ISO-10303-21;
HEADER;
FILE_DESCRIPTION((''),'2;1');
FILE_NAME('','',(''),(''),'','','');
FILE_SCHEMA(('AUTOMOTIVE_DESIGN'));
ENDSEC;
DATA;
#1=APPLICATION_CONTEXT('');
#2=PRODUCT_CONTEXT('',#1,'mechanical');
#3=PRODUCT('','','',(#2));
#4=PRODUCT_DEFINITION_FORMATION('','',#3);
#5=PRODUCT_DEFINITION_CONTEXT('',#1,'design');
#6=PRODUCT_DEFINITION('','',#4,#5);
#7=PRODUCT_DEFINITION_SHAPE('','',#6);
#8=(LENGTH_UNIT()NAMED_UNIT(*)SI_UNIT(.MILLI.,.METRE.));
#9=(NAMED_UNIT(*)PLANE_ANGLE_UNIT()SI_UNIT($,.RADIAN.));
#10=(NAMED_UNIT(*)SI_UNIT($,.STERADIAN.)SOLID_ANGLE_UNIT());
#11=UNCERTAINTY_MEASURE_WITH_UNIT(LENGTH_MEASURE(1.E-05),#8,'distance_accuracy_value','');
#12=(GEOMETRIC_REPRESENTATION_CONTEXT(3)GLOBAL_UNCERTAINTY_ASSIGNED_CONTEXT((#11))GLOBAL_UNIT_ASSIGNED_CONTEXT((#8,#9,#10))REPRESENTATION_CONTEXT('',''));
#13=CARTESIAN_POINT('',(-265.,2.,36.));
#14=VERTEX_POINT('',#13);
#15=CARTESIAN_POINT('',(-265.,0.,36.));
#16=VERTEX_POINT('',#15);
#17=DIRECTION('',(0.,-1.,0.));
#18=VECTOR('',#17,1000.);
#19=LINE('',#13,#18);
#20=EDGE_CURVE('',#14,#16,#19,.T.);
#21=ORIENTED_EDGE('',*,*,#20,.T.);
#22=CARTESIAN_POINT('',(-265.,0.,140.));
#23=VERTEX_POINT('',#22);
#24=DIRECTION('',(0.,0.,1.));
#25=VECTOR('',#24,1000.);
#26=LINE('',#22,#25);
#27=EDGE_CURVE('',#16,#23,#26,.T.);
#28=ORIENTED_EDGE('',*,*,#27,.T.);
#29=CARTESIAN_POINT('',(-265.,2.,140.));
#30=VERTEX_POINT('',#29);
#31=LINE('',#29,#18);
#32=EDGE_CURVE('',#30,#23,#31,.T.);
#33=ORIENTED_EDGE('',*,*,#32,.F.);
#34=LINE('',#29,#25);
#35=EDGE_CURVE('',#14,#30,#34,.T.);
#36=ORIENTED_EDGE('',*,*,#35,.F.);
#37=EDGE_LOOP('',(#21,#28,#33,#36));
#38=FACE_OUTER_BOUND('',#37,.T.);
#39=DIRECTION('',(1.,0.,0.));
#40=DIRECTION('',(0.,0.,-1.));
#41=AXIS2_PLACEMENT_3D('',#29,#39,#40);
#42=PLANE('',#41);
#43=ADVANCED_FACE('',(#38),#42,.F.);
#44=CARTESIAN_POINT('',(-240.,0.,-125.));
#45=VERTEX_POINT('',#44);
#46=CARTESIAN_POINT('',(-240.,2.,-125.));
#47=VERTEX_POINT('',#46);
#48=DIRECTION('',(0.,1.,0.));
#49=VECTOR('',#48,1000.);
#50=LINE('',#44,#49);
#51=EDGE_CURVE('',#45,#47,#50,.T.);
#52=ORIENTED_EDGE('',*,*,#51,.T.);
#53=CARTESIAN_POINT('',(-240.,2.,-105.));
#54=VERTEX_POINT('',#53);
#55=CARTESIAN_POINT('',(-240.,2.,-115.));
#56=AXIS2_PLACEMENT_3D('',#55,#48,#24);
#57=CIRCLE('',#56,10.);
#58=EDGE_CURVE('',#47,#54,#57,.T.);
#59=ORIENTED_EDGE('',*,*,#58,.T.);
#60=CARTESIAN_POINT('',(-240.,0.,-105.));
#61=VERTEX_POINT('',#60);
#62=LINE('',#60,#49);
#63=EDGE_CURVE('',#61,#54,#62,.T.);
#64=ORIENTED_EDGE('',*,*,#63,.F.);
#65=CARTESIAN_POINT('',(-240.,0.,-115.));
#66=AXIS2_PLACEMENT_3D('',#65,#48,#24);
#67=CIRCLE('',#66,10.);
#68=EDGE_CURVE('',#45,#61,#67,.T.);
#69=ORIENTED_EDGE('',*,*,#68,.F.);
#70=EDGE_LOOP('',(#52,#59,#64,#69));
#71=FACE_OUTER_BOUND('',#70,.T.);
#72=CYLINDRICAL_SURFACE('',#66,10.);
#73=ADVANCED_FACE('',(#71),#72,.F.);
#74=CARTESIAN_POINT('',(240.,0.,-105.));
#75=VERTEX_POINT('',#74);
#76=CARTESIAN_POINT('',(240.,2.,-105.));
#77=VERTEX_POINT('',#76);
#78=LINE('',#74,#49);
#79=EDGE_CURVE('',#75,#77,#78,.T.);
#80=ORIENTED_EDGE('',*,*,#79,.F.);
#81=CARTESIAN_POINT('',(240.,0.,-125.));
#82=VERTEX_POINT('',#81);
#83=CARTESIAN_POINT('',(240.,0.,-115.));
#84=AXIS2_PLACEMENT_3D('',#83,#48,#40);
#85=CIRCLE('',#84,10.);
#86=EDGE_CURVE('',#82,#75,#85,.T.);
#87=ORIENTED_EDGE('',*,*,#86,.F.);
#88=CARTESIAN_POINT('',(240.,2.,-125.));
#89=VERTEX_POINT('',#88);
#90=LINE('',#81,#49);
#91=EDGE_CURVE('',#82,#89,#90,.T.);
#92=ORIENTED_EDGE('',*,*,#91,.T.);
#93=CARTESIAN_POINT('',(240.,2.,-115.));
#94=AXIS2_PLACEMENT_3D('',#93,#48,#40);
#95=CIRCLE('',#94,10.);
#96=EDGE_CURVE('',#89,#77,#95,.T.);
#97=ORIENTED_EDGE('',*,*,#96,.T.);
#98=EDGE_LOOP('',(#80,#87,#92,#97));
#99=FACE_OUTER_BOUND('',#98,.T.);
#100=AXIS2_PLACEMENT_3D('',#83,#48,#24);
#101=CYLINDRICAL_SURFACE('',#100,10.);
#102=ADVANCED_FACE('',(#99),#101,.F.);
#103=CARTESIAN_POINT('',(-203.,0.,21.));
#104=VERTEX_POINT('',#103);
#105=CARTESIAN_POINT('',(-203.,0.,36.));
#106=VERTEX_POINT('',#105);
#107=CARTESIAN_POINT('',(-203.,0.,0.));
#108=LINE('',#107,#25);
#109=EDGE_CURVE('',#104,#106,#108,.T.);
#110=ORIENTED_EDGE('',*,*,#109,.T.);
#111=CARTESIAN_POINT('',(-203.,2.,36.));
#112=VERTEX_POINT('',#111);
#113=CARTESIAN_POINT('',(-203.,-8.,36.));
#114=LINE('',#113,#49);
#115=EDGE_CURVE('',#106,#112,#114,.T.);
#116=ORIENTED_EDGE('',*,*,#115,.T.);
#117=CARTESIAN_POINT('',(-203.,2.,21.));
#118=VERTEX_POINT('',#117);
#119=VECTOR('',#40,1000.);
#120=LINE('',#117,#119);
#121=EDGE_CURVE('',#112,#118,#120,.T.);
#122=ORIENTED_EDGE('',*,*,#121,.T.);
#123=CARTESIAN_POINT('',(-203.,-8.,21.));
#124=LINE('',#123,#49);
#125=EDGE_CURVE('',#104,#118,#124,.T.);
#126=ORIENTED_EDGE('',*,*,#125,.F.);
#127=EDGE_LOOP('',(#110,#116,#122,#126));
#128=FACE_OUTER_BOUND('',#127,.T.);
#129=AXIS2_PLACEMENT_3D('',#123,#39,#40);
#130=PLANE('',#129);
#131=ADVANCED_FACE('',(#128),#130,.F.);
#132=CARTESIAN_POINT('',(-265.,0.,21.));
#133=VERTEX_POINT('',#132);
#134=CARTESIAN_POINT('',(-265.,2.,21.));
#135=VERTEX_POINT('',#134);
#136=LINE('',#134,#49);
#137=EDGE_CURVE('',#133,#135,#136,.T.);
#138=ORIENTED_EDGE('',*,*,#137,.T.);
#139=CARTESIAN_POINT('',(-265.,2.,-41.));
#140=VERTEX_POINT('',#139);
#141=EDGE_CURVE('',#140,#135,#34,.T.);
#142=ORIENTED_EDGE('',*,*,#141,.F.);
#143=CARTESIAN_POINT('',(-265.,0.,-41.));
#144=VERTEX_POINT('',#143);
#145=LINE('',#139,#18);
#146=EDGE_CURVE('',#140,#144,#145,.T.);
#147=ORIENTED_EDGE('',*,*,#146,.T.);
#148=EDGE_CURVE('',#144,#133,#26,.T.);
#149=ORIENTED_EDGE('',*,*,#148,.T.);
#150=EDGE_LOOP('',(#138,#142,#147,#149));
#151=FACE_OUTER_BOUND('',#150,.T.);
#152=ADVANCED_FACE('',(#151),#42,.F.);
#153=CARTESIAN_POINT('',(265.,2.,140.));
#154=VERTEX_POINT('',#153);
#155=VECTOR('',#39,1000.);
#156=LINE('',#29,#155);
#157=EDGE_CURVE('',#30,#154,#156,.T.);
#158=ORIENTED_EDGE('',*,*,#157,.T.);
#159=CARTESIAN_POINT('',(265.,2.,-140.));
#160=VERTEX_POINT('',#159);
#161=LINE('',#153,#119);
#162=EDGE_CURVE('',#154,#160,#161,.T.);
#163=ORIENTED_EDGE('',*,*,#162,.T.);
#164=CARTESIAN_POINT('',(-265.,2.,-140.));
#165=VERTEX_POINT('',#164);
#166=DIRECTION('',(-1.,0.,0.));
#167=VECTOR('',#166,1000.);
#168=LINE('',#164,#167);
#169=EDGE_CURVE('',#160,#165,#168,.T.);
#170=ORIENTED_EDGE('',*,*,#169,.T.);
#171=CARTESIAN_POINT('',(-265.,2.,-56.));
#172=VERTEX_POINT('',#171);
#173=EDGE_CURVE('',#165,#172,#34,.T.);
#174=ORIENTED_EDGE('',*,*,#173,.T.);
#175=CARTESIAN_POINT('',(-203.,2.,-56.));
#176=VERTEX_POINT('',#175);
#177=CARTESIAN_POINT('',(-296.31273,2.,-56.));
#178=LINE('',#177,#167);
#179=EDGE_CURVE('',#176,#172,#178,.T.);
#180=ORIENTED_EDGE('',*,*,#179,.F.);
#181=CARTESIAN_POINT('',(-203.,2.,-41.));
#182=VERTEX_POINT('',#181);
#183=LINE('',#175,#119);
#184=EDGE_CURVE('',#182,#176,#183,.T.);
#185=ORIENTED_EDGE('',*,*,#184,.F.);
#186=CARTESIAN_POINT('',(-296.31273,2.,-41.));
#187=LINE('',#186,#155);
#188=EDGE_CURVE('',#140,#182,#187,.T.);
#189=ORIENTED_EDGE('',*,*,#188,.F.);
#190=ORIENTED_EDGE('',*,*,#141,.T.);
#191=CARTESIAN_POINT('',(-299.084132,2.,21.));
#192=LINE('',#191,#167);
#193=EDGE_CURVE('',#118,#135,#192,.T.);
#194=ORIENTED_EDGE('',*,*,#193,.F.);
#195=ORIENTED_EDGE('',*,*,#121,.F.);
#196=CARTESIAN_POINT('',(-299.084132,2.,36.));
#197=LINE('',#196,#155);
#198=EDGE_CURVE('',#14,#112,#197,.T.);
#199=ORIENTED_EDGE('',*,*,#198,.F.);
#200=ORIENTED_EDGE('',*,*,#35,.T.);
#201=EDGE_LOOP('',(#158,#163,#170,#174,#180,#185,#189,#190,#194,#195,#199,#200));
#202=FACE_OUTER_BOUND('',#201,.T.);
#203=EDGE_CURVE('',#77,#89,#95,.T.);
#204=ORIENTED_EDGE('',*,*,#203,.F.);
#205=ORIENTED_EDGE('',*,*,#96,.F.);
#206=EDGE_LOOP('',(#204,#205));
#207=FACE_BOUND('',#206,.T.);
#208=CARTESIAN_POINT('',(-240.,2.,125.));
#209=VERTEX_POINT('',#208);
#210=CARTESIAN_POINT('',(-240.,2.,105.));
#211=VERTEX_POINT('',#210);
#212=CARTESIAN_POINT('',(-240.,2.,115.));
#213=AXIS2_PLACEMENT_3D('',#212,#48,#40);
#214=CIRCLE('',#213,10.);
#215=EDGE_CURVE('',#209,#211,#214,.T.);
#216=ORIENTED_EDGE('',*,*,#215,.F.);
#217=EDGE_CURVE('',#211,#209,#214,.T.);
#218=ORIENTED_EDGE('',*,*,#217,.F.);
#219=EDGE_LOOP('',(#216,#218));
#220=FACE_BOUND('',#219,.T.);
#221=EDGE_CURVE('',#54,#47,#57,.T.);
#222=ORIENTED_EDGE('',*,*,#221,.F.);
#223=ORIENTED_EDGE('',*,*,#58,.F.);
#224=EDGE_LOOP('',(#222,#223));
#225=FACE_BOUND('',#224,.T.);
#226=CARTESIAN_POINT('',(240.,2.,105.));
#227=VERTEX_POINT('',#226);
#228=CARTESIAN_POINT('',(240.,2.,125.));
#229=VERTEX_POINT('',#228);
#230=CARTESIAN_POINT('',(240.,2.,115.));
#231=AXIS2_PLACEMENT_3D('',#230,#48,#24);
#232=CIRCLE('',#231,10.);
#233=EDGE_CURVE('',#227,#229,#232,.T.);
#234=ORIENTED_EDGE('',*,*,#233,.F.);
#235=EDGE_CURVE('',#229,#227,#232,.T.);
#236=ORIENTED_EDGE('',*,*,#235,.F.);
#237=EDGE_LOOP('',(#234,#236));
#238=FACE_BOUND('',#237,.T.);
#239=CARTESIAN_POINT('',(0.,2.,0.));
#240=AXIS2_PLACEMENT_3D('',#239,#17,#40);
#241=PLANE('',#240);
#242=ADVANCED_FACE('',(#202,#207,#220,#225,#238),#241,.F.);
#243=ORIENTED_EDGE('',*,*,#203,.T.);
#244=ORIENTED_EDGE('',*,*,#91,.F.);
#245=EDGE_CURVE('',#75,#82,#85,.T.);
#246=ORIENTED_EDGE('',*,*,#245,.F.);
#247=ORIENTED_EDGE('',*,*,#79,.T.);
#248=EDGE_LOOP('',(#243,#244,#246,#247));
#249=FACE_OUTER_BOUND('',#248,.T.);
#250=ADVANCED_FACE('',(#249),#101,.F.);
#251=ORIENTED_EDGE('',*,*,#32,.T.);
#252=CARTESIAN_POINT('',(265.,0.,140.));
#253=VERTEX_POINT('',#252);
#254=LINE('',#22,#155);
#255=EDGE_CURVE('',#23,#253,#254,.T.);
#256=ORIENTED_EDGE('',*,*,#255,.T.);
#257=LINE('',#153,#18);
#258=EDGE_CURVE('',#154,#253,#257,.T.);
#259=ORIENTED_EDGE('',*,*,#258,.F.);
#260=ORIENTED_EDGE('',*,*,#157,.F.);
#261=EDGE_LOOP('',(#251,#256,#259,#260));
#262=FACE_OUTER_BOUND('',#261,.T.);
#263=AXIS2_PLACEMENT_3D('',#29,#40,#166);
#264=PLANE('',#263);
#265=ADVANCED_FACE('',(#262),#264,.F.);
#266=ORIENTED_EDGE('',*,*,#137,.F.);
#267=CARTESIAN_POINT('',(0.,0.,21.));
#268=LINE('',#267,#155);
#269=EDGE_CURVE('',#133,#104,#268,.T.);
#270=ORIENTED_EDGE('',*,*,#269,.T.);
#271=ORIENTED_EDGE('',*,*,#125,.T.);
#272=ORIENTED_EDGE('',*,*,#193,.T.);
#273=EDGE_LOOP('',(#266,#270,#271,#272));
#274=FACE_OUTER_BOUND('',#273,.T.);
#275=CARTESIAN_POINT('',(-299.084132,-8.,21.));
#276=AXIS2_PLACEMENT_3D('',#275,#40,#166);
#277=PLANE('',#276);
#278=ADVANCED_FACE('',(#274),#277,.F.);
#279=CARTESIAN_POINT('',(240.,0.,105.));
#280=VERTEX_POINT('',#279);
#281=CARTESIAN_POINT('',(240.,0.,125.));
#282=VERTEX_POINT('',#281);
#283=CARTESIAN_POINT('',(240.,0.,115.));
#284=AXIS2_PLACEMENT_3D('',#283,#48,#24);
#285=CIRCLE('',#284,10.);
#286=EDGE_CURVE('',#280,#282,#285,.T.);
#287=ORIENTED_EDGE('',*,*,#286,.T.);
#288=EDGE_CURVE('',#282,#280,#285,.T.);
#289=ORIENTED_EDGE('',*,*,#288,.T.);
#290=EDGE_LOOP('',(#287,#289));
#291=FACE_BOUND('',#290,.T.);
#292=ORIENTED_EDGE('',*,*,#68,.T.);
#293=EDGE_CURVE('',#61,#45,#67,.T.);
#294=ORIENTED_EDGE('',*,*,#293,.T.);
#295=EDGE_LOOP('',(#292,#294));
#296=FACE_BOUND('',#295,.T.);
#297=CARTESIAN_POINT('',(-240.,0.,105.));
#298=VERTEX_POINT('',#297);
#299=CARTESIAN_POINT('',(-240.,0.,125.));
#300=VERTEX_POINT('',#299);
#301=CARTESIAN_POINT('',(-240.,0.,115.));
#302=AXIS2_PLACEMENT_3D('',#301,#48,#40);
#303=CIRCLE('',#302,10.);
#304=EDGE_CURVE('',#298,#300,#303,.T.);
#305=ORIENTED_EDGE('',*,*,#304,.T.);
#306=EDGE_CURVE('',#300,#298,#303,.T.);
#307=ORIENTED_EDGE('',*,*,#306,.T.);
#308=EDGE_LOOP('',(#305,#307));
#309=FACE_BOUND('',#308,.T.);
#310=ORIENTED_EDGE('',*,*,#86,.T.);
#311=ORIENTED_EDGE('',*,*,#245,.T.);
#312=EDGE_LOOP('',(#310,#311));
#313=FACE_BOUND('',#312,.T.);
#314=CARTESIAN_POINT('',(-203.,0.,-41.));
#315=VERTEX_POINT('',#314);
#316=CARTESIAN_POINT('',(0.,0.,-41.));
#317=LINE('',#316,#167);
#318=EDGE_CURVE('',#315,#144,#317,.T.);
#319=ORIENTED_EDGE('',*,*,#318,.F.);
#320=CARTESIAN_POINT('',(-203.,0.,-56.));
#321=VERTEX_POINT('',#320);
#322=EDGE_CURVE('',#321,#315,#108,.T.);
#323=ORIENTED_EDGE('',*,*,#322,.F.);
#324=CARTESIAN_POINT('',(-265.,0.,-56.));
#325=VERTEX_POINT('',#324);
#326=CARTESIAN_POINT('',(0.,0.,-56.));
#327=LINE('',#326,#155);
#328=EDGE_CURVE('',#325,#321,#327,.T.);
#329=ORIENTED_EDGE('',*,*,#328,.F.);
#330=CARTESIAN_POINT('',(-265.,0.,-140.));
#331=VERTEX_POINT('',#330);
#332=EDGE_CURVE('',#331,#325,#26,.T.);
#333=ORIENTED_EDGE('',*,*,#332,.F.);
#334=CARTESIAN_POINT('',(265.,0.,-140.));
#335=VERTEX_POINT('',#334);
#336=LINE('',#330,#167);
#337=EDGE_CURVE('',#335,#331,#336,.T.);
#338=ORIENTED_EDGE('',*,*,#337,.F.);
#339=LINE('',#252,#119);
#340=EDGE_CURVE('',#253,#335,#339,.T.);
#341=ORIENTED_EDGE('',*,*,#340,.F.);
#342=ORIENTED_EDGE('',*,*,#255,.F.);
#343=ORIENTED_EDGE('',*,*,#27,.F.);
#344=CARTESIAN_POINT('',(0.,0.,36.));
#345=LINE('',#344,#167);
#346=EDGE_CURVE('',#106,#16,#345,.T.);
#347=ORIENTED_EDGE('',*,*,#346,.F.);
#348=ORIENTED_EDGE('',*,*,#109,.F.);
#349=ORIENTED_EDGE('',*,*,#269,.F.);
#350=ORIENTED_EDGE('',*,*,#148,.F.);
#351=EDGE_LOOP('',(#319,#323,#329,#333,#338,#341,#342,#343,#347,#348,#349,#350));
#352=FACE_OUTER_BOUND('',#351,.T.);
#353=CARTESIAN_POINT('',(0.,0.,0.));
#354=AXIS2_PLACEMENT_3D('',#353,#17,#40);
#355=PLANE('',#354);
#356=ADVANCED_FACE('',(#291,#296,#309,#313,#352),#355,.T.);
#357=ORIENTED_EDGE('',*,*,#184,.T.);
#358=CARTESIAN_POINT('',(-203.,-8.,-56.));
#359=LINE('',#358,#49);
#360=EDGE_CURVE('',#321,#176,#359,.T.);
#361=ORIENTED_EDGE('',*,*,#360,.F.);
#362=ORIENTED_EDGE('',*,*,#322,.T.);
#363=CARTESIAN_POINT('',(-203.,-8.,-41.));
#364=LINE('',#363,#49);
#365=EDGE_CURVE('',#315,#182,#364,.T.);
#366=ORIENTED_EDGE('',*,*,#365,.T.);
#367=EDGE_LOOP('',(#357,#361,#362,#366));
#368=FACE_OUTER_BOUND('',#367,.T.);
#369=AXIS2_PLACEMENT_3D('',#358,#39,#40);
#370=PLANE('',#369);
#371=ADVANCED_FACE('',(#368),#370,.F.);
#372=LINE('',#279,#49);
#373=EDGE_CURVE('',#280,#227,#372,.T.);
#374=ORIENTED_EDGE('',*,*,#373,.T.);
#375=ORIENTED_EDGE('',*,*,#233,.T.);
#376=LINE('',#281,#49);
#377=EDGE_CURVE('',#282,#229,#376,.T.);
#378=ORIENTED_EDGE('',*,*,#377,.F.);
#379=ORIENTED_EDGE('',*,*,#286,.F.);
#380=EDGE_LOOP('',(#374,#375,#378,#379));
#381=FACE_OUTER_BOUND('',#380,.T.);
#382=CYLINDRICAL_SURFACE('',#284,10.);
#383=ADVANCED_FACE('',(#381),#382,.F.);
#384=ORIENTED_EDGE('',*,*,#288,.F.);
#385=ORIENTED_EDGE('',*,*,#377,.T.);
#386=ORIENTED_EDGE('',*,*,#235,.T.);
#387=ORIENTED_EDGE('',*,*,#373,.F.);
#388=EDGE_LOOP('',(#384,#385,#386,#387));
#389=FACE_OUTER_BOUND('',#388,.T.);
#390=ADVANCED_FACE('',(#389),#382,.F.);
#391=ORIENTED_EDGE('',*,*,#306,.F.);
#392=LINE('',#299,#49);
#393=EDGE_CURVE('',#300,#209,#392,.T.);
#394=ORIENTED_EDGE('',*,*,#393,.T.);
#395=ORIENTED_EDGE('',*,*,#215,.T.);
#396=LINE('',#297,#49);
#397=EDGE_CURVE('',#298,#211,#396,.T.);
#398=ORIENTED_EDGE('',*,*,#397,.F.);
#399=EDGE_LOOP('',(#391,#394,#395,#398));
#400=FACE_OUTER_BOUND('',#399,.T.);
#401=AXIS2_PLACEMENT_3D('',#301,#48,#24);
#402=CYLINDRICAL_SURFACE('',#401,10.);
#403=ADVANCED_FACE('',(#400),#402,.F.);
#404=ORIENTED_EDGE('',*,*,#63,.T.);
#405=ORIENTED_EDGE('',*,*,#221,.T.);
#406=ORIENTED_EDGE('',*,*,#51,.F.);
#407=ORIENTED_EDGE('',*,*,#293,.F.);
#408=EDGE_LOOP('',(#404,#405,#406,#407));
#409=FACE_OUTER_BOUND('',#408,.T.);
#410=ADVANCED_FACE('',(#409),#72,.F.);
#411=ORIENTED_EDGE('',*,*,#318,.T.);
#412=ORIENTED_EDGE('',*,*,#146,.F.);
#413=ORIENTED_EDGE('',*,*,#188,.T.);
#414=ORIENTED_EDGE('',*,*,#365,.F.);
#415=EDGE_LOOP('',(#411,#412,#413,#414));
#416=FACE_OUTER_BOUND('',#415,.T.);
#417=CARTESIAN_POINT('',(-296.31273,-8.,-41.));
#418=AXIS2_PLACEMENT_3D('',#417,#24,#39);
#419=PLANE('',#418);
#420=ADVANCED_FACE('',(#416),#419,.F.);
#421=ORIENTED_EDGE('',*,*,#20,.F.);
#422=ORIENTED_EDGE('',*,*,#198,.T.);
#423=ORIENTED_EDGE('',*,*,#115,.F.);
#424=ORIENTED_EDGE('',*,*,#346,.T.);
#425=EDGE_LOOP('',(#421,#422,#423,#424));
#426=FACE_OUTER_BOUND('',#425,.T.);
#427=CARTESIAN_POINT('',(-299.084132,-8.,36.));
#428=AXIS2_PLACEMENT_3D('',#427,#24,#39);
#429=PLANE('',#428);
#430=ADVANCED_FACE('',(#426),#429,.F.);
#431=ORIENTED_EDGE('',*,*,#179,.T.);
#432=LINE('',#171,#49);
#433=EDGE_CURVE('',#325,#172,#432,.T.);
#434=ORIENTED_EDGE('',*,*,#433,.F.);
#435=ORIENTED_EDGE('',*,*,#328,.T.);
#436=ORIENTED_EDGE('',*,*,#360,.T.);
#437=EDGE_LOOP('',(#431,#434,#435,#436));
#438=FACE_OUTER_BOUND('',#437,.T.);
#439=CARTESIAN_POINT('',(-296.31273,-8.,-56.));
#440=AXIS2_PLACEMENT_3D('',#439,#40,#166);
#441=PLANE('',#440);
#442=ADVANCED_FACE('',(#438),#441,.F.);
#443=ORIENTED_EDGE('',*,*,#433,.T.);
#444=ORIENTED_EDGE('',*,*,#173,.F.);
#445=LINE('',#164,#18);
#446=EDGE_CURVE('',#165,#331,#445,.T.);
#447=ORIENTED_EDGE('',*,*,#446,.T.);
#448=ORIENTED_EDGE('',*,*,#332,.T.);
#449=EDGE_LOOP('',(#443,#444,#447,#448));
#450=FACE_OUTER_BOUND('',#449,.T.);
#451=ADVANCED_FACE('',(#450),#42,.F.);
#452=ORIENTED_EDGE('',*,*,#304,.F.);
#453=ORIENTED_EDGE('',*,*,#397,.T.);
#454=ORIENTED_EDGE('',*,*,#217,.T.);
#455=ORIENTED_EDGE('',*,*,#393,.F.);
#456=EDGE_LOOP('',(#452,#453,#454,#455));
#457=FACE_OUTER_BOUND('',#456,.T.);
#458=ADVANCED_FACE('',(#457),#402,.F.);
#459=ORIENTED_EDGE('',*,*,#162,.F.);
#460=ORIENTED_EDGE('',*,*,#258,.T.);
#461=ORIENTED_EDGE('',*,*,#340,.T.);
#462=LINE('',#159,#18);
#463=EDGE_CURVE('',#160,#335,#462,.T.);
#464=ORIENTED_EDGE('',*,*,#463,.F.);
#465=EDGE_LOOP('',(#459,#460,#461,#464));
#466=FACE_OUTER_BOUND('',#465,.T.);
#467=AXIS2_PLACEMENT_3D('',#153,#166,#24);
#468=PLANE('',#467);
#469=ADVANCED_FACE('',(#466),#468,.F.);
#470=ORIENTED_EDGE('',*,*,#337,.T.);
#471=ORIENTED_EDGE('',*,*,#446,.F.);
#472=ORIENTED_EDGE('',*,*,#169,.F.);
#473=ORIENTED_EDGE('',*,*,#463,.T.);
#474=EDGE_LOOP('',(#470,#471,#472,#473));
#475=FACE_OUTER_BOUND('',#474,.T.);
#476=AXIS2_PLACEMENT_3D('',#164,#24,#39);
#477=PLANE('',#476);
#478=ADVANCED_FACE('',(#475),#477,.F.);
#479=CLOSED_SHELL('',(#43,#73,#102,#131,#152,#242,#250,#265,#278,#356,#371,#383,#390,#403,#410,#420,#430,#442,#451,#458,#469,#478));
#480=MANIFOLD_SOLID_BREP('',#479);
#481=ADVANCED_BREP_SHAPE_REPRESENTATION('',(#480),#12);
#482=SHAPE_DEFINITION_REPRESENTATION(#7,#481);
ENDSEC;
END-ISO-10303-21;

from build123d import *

# Parameters (mm, degrees)
SKETCH_1_W          = 530
SKETCH_1_H          = 280
EXTRUDE_1_DEPTH     = 2
SKETCH_2_R          = 10
CUT_EXTRUDE_1_DEPTH = 2
SKETCH_3_W          = 96.084131949
SKETCH_3_H          = 15
SKETCH_3_W_2        = 93.312729878
CUT_EXTRUDE_2_DEPTH = 10


with BuildPart() as part:
    # 草图1 → 凸台-拉伸1 (new body)
    with BuildSketch(Plane(origin=(0, 0, 0), x_dir=(1, 0, 0), z_dir=(0, 1, 0))):
        Rectangle(SKETCH_1_W, SKETCH_1_H)
    extrude(amount=EXTRUDE_1_DEPTH)

    # 草图2 → 切除-拉伸1 (cut)
    with BuildSketch(Plane(origin=(0, 2, 0), x_dir=(1, 0, 0), z_dir=(0, 1, 0))):
        with Locations(Location((-240, 115, 0), (0, 0, 270))):
            Circle(SKETCH_2_R)
        with Locations(Location((-240, -115, 0), (0, 0, 90))):
            Circle(SKETCH_2_R)
        with Locations(Location((240, -115, 0), (0, 0, 270))):
            Circle(SKETCH_2_R)
        with Locations(Location((240, 115, 0), (0, 0, 90))):
            Circle(SKETCH_2_R)
    extrude(amount=-CUT_EXTRUDE_1_DEPTH, mode=Mode.SUBTRACT)

    # 草图3 → 切除-拉伸2 (cut)
    with BuildSketch(Plane(origin=(0, 2, 0), x_dir=(1, 0, 0), z_dir=(0, 1, 0))):
        with Locations((-251.042065975, -28.5)):
            Rectangle(SKETCH_3_W, SKETCH_3_H)
        with Locations((-249.656364939, 48.5)):
            Rectangle(SKETCH_3_W_2, SKETCH_3_H)
    extrude(amount=-CUT_EXTRUDE_2_DEPTH, mode=Mode.SUBTRACT)


solid = part.part
